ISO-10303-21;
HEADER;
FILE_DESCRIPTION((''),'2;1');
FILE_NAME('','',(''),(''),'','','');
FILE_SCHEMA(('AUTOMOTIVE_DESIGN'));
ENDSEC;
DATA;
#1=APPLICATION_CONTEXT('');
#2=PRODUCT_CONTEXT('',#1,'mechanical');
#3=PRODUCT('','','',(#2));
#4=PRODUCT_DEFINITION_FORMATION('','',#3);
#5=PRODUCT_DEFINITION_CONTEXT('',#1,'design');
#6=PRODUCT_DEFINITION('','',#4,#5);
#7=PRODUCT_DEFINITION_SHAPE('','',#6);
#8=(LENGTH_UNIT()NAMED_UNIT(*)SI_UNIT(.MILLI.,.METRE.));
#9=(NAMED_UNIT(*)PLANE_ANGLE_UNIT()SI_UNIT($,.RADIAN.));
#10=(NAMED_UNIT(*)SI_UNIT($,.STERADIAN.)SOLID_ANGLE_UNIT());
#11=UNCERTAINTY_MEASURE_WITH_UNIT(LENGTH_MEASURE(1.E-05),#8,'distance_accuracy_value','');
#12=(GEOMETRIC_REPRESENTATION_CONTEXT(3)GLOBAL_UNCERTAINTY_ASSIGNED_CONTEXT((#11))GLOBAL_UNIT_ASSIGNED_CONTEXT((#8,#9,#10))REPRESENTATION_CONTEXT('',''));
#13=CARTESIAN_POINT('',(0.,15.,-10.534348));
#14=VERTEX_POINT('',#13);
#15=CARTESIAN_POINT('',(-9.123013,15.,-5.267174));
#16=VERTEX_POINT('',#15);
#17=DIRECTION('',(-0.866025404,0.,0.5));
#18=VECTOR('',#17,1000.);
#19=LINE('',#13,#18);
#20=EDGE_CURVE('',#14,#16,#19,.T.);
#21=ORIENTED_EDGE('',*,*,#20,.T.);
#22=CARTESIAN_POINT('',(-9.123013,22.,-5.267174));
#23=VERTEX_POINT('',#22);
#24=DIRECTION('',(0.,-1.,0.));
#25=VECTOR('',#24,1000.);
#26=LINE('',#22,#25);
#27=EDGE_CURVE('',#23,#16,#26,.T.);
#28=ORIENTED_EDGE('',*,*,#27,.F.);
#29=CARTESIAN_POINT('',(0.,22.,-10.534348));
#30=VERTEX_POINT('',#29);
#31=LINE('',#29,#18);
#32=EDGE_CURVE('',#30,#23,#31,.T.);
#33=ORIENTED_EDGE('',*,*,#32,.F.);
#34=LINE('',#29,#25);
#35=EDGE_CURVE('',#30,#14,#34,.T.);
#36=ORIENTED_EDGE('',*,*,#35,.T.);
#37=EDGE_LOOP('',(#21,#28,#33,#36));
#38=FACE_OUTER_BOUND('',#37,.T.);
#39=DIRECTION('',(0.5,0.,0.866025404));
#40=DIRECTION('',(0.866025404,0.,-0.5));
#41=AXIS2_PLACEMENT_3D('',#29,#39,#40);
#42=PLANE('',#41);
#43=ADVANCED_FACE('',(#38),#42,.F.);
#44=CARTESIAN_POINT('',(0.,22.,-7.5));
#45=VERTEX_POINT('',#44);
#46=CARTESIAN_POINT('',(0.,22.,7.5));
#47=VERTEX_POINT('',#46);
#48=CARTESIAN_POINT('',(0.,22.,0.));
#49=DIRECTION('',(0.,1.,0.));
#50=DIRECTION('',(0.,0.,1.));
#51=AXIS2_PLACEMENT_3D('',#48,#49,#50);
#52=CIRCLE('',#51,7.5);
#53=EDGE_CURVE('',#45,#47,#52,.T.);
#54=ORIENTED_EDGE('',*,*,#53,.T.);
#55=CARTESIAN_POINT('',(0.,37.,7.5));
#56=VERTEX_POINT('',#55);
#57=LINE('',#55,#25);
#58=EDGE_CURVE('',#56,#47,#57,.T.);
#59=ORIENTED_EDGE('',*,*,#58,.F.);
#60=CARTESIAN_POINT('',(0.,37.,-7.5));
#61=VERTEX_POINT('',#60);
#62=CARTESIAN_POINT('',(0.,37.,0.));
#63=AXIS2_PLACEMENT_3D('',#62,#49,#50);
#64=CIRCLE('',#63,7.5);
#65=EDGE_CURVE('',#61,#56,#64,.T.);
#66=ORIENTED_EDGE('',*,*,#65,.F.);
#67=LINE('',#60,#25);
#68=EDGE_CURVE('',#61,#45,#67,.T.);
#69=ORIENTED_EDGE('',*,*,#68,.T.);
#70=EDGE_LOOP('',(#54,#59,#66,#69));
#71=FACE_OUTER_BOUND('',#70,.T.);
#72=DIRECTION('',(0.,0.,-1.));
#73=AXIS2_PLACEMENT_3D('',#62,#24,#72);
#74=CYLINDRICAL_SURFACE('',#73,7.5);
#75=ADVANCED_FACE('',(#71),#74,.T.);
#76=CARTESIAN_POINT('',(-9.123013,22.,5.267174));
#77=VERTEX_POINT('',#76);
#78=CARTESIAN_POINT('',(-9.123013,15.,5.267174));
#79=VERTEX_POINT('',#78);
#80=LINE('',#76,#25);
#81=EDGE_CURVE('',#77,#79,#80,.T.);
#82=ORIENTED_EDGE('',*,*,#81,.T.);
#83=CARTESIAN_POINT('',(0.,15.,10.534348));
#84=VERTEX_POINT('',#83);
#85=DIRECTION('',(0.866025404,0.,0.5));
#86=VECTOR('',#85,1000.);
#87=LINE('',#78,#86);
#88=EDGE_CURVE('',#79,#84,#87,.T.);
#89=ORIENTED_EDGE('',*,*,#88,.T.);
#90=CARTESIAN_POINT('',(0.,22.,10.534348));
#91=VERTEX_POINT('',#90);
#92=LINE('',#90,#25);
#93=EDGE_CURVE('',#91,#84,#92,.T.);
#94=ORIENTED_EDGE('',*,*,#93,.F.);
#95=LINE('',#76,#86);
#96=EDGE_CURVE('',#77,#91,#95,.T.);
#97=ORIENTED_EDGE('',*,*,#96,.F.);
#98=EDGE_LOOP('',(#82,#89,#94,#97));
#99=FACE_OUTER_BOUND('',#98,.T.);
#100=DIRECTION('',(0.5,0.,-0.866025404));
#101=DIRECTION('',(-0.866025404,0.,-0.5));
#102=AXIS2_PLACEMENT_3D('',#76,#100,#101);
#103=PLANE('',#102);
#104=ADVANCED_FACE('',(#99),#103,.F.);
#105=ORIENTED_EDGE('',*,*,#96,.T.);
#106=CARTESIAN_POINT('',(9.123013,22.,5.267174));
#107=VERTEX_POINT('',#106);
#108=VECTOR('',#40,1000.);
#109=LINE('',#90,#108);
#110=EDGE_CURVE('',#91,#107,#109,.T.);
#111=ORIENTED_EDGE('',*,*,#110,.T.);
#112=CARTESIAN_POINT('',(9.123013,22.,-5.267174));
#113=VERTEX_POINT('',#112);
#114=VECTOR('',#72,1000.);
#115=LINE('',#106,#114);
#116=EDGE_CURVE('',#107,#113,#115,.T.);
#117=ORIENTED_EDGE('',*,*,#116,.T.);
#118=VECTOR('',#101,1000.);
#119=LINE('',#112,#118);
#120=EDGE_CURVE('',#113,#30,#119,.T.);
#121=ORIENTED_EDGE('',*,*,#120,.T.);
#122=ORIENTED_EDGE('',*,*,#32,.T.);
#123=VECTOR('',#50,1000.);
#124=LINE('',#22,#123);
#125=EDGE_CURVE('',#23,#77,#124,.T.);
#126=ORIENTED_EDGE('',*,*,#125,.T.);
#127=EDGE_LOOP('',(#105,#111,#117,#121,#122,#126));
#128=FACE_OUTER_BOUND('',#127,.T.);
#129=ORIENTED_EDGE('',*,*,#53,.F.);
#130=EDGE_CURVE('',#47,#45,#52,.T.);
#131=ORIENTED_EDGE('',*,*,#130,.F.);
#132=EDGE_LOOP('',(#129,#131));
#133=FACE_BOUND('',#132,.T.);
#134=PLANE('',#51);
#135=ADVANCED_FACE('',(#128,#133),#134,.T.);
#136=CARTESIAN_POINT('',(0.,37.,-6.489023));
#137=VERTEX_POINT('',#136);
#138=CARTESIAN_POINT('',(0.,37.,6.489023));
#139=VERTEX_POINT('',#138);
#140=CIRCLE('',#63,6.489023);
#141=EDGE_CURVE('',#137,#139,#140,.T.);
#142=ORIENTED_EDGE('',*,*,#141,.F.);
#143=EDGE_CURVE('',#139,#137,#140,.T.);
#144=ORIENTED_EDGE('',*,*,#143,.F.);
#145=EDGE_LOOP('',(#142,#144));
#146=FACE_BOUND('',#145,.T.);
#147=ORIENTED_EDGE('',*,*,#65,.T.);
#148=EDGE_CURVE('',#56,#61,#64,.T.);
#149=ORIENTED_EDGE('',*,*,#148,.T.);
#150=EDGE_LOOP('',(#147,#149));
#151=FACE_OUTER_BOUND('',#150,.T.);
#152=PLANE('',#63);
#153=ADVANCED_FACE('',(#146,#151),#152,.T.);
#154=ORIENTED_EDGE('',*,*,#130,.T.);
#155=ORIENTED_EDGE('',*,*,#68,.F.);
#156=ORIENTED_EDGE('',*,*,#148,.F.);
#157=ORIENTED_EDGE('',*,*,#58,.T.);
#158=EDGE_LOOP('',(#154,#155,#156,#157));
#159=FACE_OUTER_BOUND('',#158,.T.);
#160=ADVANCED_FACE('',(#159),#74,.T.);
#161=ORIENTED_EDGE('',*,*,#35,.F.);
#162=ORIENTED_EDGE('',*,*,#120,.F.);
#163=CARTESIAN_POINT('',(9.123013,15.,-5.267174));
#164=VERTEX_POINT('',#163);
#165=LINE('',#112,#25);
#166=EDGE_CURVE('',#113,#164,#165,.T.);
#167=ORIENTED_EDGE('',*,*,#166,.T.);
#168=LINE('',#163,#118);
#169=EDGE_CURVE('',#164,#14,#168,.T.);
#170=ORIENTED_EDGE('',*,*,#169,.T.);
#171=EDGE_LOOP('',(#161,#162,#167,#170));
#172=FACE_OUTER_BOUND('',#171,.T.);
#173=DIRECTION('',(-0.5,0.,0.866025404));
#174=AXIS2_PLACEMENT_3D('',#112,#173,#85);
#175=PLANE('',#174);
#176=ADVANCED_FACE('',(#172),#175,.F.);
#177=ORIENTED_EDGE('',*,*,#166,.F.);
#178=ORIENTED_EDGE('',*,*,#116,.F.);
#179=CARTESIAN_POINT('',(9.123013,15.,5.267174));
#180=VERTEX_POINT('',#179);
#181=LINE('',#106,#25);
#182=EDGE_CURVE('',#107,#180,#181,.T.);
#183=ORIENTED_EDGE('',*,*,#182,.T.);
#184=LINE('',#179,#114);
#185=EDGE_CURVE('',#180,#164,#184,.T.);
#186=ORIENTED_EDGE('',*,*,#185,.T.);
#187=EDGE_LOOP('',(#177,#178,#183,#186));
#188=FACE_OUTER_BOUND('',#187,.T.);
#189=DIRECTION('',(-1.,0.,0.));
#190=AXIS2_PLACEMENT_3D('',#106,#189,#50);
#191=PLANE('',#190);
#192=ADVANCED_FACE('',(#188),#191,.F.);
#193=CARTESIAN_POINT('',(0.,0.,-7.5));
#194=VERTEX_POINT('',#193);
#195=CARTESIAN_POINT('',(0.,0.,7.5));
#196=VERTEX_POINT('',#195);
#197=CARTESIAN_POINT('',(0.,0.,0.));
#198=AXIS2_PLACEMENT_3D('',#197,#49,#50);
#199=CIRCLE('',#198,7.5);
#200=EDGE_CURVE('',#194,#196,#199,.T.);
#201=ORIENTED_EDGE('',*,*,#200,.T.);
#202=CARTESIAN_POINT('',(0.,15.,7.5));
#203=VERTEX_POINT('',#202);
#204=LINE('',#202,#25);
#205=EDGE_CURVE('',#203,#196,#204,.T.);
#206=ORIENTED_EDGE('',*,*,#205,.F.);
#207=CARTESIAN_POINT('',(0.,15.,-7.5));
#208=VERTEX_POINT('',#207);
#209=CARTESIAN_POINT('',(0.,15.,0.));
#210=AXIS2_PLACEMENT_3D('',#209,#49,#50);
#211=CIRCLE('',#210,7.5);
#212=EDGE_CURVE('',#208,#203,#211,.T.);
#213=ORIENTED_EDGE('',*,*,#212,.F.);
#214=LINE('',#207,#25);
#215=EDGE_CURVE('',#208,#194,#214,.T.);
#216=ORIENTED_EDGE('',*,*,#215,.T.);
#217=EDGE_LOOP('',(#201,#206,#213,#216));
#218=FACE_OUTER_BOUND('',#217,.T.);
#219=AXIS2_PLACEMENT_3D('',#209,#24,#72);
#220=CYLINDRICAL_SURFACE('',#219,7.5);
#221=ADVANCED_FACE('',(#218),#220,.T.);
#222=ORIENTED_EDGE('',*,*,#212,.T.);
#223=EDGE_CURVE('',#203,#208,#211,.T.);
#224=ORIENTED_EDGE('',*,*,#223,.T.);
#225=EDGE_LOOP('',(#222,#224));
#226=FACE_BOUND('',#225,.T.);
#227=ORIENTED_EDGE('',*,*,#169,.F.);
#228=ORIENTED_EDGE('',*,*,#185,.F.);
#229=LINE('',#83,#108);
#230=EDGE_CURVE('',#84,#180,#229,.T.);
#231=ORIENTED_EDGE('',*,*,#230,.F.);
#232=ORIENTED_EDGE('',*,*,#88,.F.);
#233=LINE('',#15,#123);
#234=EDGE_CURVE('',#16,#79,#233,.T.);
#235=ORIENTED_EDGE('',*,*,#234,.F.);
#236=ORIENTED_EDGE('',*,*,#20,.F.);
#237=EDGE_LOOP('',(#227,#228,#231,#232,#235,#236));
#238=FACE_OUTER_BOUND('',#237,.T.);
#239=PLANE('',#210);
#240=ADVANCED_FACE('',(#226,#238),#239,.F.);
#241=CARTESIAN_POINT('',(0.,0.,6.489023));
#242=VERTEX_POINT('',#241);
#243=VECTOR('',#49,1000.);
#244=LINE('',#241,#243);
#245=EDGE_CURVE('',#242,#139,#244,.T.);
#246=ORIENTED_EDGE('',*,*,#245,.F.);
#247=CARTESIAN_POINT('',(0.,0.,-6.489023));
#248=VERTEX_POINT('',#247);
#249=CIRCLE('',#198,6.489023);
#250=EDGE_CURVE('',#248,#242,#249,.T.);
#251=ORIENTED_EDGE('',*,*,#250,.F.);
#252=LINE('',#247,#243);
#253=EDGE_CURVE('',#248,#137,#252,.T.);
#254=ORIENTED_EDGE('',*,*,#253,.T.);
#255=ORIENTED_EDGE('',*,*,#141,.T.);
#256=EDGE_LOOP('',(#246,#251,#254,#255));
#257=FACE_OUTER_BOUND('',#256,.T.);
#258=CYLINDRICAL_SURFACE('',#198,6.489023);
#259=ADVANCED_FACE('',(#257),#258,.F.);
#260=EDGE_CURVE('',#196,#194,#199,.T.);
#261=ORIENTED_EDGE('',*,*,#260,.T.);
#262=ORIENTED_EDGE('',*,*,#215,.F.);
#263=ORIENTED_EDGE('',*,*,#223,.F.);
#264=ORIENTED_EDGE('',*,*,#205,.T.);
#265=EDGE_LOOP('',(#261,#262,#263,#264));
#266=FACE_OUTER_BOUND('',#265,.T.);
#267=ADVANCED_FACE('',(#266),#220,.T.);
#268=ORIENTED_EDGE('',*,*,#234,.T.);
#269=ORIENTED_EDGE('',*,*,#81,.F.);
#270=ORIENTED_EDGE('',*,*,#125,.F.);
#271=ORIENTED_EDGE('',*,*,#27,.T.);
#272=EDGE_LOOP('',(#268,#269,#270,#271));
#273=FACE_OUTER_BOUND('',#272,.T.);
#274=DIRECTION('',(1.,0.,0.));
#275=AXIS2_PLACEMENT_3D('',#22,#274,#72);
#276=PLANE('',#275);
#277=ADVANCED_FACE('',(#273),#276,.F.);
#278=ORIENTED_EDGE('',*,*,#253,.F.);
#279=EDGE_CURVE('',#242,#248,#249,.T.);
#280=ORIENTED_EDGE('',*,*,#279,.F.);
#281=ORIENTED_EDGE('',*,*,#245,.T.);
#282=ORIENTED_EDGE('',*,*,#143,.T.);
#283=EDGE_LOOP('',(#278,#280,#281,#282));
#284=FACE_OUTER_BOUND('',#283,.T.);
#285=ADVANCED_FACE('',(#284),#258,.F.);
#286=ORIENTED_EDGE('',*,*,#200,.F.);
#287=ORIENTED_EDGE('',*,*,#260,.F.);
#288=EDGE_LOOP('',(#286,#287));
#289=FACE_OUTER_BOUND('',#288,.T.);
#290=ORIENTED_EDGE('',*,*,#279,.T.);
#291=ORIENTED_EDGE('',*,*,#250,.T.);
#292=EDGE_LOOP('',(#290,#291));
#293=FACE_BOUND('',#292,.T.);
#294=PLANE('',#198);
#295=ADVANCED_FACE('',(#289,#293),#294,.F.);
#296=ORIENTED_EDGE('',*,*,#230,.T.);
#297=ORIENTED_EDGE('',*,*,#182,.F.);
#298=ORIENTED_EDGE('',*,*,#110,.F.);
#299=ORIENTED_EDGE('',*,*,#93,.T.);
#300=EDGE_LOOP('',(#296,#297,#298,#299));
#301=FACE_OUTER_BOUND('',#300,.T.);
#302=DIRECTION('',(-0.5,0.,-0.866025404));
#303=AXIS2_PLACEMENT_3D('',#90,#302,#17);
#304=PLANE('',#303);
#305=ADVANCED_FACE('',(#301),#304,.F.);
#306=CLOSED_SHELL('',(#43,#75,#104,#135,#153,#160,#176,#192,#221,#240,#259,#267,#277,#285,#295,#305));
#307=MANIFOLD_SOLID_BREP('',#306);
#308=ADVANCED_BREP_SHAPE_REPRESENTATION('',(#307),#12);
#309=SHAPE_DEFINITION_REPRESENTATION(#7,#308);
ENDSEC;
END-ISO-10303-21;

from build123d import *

# Parameters (mm, degrees)
SKETCH1_R           = 7.5
BOSS_EXTRUDE1_DEPTH = 15
BOSS_EXTRUDE2_DEPTH = 7
SKETCH3_R           = 7.5
BOSS_EXTRUDE3_DEPTH = 15
SKETCH4_R           = 6.489023352
CUT_EXTRUDE1_DEPTH  = 40.537347476


with BuildPart() as part:
    # Sketch1 → Boss-Extrude1 (new body)
    with BuildSketch(Plane(origin=(0, 0, 0), x_dir=(1, 0, 0), z_dir=(0, 1, 0))):
        with Locations(Location((0, 0, 0), (0, 0, 270))):
            Circle(SKETCH1_R)
    extrude(amount=BOSS_EXTRUDE1_DEPTH)

    # Sketch2 → Boss-Extrude2 (add)
    with BuildSketch(Plane(origin=(0, 15, 0), x_dir=(1, 0, 0), z_dir=(0, 1, 0))):
        Polygon((-9.123012787, 5.267173889), (-9.123012787, -5.267173889), (0, -10.534347777), (9.123012787, -5.267173889), (9.123012787, 5.267173889), (0, 10.534347777), align=None)
    extrude(amount=BOSS_EXTRUDE2_DEPTH)

    # Sketch3 → Boss-Extrude3 (add)
    with BuildSketch(Plane(origin=(0, 22, 0), x_dir=(1, 0, 0), z_dir=(0, 1, 0))):
        with Locations(Location((0, 0, 0), (0, 0, 270))):
            Circle(SKETCH3_R)
    extrude(amount=BOSS_EXTRUDE3_DEPTH)

    # Sketch4 → Cut-Extrude1 (cut, through all)
    with BuildSketch(Plane(origin=(0, 37, 0), x_dir=(1, 0, 0), z_dir=(0, 1, 0))):
        with Locations(Location((0, 0, 0), (0, 0, 270))):
            Circle(SKETCH4_R)
    extrude(amount=-CUT_EXTRUDE1_DEPTH, mode=Mode.SUBTRACT)


solid = part.part
